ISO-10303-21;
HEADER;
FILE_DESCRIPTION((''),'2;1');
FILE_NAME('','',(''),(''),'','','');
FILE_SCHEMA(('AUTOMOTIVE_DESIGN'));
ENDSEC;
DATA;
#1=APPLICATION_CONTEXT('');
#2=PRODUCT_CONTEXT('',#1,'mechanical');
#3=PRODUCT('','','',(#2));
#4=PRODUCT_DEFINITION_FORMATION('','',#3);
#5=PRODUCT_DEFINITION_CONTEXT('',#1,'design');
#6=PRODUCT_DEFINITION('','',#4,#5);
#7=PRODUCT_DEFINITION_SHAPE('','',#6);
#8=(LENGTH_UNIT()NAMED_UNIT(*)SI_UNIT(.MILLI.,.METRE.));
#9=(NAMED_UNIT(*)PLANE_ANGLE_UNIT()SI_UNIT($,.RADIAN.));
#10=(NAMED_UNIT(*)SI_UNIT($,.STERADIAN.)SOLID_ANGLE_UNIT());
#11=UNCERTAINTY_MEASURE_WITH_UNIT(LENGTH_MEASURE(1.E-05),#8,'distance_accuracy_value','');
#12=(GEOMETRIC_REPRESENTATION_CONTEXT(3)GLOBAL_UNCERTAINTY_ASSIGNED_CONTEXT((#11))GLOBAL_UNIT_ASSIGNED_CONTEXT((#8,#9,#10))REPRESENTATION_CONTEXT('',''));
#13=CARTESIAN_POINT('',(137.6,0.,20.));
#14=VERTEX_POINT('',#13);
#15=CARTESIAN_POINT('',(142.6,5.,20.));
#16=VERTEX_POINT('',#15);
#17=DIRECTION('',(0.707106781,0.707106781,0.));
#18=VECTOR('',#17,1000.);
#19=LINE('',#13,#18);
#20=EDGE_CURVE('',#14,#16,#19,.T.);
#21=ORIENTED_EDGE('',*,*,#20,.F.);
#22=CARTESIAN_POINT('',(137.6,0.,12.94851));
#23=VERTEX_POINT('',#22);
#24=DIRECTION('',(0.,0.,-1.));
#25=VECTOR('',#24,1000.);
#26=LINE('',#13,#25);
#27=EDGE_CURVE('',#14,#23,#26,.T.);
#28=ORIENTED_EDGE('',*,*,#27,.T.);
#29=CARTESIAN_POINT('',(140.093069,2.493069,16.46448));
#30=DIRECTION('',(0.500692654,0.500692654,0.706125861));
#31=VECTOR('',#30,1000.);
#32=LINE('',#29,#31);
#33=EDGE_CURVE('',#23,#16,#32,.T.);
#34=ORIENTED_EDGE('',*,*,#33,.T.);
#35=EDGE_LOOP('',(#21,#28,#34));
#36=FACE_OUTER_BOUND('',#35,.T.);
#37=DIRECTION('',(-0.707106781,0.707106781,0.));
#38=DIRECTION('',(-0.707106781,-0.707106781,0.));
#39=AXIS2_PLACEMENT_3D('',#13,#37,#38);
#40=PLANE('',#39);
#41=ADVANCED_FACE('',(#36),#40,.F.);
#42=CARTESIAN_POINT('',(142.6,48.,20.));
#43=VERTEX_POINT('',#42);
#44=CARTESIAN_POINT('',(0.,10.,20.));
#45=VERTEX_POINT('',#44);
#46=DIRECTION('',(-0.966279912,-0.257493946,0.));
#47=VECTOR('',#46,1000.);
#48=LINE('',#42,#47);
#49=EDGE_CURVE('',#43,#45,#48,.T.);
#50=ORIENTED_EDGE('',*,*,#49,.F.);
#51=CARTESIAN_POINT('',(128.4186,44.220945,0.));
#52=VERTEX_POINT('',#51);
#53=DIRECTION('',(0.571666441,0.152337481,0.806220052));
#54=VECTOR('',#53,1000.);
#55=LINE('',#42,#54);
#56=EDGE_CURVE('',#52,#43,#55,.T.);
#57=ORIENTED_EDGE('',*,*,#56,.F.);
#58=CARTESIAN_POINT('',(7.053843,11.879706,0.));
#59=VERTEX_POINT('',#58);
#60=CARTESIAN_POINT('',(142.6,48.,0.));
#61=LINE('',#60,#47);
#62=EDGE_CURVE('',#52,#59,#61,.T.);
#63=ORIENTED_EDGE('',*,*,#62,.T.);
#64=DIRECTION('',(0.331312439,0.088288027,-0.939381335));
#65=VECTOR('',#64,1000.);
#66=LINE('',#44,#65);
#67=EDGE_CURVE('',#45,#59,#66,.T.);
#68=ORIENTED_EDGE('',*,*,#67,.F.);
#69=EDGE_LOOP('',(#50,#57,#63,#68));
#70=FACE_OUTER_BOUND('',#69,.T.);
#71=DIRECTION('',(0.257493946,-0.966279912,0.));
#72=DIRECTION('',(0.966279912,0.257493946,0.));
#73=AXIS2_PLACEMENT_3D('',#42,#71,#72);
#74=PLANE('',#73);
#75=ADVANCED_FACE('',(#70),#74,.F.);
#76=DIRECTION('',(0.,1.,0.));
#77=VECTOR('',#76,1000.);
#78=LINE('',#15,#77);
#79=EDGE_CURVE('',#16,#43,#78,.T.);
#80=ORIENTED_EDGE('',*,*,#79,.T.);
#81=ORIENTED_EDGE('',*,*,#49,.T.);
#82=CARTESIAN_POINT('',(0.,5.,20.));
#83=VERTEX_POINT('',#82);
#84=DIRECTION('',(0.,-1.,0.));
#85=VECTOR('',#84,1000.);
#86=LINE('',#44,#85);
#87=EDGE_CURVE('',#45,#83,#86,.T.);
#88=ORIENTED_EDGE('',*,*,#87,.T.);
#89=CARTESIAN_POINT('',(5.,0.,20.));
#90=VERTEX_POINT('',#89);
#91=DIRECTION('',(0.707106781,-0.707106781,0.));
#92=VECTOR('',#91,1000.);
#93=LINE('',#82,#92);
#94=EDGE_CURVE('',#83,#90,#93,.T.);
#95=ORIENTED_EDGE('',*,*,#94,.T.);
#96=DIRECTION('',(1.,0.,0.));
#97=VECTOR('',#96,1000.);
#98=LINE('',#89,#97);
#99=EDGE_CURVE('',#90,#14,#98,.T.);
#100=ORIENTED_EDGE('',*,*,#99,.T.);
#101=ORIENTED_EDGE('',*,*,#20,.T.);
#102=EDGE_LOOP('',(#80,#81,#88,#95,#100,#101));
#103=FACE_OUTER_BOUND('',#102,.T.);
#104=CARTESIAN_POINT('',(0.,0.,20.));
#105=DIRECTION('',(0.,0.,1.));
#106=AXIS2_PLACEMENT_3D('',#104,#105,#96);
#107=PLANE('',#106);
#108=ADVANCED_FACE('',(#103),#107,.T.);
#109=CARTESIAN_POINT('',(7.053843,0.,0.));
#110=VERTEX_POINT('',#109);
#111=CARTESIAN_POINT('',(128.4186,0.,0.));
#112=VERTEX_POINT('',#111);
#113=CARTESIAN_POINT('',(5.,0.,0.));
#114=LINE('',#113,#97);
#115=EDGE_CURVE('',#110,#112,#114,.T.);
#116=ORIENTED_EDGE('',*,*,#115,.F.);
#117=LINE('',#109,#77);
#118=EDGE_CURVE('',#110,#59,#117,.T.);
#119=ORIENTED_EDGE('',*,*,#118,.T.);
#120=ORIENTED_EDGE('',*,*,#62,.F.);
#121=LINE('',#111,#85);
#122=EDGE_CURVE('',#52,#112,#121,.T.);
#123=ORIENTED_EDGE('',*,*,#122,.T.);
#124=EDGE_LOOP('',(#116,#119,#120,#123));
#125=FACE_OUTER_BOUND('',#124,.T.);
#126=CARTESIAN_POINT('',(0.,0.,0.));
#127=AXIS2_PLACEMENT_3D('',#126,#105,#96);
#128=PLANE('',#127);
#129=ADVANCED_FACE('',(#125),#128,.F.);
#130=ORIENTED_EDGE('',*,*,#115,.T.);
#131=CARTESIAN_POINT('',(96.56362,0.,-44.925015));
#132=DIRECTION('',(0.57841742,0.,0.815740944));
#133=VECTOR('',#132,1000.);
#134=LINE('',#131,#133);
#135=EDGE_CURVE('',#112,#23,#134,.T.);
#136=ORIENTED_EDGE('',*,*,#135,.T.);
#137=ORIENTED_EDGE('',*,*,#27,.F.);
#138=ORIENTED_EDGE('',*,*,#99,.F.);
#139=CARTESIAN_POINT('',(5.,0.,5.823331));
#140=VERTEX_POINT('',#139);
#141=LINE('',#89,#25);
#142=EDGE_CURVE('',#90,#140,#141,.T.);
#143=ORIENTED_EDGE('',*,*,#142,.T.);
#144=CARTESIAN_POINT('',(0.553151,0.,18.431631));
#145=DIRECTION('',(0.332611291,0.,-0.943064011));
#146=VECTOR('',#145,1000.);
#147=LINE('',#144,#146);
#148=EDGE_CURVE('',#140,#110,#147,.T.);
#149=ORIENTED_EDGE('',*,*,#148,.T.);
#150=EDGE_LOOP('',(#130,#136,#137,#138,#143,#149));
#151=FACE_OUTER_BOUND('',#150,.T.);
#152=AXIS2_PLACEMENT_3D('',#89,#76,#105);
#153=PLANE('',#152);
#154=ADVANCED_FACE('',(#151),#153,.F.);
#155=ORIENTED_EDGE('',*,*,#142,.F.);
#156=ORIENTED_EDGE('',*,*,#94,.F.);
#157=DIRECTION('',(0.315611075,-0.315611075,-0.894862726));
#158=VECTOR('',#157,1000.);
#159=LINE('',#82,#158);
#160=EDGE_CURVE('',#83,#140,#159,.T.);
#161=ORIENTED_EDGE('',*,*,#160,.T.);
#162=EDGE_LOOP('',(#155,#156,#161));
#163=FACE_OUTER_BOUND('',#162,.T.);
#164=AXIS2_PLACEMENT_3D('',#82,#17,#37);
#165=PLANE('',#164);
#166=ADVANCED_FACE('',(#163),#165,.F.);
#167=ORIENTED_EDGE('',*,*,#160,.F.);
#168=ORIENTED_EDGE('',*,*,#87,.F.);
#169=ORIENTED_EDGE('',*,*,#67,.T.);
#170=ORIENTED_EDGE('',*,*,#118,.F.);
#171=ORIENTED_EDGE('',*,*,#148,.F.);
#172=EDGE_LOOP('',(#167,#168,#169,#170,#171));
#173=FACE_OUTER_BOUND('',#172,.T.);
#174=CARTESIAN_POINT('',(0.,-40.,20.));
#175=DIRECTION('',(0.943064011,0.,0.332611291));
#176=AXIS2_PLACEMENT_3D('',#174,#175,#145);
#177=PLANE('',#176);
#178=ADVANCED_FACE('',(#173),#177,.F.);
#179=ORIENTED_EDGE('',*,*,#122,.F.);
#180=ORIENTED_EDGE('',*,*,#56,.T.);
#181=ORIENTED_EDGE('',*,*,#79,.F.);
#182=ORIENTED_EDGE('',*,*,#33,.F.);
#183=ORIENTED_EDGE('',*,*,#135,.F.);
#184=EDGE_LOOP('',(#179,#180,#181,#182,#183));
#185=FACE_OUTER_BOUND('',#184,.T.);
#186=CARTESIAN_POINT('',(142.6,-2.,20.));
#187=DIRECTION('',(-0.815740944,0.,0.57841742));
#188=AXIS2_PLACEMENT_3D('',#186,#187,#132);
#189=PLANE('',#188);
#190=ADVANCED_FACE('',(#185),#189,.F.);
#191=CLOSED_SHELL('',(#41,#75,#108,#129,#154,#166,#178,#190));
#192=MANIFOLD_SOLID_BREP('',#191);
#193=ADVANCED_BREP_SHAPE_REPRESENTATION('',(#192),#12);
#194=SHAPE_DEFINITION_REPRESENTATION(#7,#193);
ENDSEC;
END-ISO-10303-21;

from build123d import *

# Parameters (mm, degrees)
BOSS_EXTRUDE1_DEPTH = 20
CUT_EXTRUDE2_DEPTH  = 50


with BuildPart() as part:
    # Sketch1 → Boss-Extrude1 (new body)
    with BuildSketch(Plane.XY):
        Polygon((5, 0), (137.6, 0), (142.6, 5), (142.6, 48), (0, 10), (0, 5), align=None)
    extrude(amount=BOSS_EXTRUDE1_DEPTH)

    # Sketch2 → Cut-Extrude2 (cut, along a direction that is not the sketch's normal)
    with BuildSketch(Plane(origin=(-2.488112271, 9.33696868, 0), x_dir=(0.9662799118048497, 0.25749394564224604, 0), z_dir=(-0.257493945642246, 0.9662799118048496, 0))):
        Polygon((2.574939456, -20), (9.874939456, 0), (2.574939456, 0), align=None)
        Polygon((150.151224814, -20), (135.474939456, 0), (150.151224814, 0), align=None)
    extrude(amount=-CUT_EXTRUDE2_DEPTH, dir=(0, 1, 0), mode=Mode.SUBTRACT)


solid = part.part
